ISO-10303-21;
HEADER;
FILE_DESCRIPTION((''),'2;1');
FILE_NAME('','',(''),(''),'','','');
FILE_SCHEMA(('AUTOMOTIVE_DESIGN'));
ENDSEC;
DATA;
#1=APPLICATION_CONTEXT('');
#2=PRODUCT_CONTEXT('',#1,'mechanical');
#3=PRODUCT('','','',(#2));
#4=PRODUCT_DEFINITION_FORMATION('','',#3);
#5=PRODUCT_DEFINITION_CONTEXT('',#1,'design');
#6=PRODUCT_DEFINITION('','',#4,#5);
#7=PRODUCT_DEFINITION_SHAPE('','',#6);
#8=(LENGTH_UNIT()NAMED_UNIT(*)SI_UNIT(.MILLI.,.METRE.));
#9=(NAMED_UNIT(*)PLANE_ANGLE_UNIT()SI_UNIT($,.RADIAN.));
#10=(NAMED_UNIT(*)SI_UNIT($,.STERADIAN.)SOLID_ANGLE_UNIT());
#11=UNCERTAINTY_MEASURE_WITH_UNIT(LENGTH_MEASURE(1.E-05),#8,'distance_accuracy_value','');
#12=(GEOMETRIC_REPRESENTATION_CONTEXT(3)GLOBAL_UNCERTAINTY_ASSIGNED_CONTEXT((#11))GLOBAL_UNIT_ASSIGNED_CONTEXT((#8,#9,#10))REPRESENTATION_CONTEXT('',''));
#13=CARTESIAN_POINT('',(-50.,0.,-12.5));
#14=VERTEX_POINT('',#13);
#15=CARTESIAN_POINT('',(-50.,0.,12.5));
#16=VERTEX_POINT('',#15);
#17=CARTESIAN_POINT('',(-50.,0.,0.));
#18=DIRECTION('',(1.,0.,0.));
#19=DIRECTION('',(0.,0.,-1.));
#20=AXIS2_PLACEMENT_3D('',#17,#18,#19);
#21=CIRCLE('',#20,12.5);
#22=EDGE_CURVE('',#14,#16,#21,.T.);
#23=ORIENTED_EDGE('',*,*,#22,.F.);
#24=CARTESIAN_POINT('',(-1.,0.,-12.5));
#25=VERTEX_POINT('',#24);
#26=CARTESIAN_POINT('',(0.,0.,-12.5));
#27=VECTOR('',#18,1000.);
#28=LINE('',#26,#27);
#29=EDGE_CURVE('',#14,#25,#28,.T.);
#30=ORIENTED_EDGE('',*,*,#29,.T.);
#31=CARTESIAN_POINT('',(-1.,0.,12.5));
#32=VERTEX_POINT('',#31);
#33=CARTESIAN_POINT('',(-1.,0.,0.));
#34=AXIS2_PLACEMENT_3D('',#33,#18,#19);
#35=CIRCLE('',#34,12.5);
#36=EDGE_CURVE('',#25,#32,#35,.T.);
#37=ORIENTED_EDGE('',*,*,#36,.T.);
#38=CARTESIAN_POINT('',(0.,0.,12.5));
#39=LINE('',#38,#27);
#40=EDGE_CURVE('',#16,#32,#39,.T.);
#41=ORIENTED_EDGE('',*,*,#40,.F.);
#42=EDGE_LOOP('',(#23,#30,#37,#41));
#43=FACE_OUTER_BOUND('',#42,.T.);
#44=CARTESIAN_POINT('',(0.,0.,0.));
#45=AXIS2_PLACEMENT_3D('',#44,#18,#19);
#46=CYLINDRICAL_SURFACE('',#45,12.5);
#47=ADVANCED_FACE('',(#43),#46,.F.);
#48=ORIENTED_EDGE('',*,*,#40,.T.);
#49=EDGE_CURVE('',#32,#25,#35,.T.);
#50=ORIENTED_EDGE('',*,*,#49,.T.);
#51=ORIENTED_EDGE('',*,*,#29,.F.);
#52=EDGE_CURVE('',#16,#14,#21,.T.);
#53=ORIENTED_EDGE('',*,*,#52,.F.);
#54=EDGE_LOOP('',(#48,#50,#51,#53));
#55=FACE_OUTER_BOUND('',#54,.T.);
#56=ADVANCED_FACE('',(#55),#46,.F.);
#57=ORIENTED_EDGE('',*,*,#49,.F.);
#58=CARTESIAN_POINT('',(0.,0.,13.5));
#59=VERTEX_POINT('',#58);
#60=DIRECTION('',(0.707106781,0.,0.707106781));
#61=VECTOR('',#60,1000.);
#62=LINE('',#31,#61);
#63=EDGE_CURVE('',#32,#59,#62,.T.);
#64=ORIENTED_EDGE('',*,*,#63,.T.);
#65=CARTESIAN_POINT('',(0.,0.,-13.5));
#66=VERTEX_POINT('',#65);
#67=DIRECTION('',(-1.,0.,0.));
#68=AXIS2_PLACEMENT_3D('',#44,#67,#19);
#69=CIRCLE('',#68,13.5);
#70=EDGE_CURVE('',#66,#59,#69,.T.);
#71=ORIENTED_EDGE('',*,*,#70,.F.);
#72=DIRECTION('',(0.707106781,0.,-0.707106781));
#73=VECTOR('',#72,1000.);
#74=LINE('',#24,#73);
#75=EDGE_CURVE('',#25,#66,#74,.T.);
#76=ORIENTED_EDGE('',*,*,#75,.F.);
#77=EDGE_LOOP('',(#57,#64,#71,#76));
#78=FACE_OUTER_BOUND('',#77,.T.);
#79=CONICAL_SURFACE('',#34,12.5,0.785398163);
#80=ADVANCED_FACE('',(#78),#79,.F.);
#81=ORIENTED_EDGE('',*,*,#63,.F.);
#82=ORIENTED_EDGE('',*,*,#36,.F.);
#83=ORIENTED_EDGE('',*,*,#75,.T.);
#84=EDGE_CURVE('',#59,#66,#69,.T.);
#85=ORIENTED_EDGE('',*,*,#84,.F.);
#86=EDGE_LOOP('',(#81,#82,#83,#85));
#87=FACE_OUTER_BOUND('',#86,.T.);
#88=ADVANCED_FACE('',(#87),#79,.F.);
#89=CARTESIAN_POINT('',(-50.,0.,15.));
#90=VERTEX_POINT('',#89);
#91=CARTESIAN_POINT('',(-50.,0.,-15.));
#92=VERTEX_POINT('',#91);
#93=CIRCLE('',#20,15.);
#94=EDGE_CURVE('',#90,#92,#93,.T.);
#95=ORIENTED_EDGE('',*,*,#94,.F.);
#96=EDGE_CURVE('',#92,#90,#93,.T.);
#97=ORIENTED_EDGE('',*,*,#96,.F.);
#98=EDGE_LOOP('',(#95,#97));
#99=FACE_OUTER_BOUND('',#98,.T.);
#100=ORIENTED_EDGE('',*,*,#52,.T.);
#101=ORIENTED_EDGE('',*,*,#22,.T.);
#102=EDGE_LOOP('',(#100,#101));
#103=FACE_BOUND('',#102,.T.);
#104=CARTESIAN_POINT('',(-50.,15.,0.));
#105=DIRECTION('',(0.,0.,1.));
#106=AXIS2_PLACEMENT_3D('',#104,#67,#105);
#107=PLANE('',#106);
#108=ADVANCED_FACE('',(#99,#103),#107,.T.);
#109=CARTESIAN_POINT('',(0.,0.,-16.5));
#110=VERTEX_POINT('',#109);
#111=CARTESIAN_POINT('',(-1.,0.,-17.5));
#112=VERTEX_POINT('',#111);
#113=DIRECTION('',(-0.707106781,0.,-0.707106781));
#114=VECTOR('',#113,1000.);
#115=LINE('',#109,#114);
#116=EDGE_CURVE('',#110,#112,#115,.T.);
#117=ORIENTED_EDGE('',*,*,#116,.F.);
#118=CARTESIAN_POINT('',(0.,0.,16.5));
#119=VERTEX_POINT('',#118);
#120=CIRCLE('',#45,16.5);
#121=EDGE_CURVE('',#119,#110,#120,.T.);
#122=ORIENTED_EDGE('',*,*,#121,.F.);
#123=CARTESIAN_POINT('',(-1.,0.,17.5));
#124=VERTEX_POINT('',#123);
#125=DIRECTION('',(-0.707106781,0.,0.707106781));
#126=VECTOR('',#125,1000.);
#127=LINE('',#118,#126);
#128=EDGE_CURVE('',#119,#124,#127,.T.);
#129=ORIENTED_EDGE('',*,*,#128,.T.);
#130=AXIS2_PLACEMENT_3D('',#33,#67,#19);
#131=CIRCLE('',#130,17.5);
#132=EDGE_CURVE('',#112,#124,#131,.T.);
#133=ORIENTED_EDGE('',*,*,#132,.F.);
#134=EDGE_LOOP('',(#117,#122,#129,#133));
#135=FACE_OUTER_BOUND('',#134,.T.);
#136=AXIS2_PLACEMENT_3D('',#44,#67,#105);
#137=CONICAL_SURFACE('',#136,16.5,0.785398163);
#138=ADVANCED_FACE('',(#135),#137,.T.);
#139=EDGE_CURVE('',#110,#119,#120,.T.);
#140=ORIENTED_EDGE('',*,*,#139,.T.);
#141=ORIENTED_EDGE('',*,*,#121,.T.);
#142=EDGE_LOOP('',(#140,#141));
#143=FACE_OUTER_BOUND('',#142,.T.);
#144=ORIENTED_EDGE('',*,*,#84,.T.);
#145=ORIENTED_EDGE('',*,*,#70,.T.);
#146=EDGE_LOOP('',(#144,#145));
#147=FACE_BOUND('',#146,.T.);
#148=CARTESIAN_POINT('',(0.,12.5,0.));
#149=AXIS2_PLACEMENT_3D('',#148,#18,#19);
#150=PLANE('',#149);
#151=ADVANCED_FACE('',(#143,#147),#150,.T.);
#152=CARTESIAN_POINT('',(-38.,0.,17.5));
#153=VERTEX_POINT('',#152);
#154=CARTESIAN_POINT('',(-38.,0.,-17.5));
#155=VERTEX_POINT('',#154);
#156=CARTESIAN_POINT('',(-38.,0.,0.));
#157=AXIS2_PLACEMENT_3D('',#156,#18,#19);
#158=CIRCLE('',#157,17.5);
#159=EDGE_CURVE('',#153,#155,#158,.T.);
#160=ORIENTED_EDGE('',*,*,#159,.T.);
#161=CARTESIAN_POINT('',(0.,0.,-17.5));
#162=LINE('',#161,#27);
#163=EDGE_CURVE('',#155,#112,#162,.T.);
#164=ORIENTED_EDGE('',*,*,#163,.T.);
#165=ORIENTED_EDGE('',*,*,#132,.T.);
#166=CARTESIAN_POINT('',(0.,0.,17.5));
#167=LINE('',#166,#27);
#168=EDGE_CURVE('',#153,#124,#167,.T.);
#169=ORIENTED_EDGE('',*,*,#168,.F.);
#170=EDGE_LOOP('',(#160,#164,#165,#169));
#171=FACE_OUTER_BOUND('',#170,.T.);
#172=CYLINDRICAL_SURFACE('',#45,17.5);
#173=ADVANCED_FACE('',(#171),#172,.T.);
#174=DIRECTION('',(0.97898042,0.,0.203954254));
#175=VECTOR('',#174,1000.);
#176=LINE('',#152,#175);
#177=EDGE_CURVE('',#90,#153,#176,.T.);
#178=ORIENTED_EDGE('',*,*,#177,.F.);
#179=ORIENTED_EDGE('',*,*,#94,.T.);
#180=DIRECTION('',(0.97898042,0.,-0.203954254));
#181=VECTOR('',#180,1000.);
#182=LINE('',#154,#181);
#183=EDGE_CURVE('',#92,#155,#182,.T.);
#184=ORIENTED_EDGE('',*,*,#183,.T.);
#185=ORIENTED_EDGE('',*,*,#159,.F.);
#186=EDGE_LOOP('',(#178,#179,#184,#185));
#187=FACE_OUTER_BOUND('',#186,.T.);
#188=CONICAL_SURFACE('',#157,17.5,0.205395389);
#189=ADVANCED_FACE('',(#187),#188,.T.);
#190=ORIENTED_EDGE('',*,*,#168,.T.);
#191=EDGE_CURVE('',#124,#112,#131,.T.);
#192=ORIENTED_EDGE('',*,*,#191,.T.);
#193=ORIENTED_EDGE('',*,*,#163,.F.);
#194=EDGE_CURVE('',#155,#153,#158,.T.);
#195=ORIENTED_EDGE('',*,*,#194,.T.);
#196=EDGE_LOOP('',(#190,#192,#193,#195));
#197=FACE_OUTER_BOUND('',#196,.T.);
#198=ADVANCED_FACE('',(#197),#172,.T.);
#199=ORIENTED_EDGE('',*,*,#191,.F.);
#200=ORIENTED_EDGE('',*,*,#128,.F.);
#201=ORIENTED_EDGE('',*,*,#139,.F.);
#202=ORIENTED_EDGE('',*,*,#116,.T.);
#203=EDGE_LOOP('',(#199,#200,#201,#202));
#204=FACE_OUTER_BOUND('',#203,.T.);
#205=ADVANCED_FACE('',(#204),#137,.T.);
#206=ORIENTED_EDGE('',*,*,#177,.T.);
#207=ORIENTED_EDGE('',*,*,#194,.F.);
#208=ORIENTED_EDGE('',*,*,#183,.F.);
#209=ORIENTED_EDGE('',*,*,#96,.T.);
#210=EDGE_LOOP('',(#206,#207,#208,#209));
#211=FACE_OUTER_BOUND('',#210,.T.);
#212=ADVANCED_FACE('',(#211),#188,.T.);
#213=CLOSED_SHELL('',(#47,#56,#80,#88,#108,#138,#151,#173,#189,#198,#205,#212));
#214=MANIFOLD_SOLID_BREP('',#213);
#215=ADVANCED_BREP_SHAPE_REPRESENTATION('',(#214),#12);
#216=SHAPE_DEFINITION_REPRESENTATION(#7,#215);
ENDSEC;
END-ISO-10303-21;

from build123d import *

# Parameters (mm, degrees)
CHAMFER1_SIZE = 1


with BuildPart() as part:
    # Sketch1 → Revolve1 (revolve)
    with BuildSketch(Plane.XY, mode=Mode.PRIVATE) as revolve1_sk:
        Polygon((0, 12.5), (0, 17.5), (-38, 17.5), (-50, 15), (-50, 12.5), align=None)
    revolve(revolve1_sk.sketch.rotate(Axis((0, 0, 0), (-1, 0, 0)), 90), axis=Axis((0, 0, 0), (-1, 0, 0)))

    # Chamfer1
    chamfer1_edges = [part.edges().sort_by_distance(p)[0] for p in [
        (0, 0, 17.5),
        (0, 0, 12.5),
    ]]
    chamfer(chamfer1_edges, length=CHAMFER1_SIZE)


solid = part.part
